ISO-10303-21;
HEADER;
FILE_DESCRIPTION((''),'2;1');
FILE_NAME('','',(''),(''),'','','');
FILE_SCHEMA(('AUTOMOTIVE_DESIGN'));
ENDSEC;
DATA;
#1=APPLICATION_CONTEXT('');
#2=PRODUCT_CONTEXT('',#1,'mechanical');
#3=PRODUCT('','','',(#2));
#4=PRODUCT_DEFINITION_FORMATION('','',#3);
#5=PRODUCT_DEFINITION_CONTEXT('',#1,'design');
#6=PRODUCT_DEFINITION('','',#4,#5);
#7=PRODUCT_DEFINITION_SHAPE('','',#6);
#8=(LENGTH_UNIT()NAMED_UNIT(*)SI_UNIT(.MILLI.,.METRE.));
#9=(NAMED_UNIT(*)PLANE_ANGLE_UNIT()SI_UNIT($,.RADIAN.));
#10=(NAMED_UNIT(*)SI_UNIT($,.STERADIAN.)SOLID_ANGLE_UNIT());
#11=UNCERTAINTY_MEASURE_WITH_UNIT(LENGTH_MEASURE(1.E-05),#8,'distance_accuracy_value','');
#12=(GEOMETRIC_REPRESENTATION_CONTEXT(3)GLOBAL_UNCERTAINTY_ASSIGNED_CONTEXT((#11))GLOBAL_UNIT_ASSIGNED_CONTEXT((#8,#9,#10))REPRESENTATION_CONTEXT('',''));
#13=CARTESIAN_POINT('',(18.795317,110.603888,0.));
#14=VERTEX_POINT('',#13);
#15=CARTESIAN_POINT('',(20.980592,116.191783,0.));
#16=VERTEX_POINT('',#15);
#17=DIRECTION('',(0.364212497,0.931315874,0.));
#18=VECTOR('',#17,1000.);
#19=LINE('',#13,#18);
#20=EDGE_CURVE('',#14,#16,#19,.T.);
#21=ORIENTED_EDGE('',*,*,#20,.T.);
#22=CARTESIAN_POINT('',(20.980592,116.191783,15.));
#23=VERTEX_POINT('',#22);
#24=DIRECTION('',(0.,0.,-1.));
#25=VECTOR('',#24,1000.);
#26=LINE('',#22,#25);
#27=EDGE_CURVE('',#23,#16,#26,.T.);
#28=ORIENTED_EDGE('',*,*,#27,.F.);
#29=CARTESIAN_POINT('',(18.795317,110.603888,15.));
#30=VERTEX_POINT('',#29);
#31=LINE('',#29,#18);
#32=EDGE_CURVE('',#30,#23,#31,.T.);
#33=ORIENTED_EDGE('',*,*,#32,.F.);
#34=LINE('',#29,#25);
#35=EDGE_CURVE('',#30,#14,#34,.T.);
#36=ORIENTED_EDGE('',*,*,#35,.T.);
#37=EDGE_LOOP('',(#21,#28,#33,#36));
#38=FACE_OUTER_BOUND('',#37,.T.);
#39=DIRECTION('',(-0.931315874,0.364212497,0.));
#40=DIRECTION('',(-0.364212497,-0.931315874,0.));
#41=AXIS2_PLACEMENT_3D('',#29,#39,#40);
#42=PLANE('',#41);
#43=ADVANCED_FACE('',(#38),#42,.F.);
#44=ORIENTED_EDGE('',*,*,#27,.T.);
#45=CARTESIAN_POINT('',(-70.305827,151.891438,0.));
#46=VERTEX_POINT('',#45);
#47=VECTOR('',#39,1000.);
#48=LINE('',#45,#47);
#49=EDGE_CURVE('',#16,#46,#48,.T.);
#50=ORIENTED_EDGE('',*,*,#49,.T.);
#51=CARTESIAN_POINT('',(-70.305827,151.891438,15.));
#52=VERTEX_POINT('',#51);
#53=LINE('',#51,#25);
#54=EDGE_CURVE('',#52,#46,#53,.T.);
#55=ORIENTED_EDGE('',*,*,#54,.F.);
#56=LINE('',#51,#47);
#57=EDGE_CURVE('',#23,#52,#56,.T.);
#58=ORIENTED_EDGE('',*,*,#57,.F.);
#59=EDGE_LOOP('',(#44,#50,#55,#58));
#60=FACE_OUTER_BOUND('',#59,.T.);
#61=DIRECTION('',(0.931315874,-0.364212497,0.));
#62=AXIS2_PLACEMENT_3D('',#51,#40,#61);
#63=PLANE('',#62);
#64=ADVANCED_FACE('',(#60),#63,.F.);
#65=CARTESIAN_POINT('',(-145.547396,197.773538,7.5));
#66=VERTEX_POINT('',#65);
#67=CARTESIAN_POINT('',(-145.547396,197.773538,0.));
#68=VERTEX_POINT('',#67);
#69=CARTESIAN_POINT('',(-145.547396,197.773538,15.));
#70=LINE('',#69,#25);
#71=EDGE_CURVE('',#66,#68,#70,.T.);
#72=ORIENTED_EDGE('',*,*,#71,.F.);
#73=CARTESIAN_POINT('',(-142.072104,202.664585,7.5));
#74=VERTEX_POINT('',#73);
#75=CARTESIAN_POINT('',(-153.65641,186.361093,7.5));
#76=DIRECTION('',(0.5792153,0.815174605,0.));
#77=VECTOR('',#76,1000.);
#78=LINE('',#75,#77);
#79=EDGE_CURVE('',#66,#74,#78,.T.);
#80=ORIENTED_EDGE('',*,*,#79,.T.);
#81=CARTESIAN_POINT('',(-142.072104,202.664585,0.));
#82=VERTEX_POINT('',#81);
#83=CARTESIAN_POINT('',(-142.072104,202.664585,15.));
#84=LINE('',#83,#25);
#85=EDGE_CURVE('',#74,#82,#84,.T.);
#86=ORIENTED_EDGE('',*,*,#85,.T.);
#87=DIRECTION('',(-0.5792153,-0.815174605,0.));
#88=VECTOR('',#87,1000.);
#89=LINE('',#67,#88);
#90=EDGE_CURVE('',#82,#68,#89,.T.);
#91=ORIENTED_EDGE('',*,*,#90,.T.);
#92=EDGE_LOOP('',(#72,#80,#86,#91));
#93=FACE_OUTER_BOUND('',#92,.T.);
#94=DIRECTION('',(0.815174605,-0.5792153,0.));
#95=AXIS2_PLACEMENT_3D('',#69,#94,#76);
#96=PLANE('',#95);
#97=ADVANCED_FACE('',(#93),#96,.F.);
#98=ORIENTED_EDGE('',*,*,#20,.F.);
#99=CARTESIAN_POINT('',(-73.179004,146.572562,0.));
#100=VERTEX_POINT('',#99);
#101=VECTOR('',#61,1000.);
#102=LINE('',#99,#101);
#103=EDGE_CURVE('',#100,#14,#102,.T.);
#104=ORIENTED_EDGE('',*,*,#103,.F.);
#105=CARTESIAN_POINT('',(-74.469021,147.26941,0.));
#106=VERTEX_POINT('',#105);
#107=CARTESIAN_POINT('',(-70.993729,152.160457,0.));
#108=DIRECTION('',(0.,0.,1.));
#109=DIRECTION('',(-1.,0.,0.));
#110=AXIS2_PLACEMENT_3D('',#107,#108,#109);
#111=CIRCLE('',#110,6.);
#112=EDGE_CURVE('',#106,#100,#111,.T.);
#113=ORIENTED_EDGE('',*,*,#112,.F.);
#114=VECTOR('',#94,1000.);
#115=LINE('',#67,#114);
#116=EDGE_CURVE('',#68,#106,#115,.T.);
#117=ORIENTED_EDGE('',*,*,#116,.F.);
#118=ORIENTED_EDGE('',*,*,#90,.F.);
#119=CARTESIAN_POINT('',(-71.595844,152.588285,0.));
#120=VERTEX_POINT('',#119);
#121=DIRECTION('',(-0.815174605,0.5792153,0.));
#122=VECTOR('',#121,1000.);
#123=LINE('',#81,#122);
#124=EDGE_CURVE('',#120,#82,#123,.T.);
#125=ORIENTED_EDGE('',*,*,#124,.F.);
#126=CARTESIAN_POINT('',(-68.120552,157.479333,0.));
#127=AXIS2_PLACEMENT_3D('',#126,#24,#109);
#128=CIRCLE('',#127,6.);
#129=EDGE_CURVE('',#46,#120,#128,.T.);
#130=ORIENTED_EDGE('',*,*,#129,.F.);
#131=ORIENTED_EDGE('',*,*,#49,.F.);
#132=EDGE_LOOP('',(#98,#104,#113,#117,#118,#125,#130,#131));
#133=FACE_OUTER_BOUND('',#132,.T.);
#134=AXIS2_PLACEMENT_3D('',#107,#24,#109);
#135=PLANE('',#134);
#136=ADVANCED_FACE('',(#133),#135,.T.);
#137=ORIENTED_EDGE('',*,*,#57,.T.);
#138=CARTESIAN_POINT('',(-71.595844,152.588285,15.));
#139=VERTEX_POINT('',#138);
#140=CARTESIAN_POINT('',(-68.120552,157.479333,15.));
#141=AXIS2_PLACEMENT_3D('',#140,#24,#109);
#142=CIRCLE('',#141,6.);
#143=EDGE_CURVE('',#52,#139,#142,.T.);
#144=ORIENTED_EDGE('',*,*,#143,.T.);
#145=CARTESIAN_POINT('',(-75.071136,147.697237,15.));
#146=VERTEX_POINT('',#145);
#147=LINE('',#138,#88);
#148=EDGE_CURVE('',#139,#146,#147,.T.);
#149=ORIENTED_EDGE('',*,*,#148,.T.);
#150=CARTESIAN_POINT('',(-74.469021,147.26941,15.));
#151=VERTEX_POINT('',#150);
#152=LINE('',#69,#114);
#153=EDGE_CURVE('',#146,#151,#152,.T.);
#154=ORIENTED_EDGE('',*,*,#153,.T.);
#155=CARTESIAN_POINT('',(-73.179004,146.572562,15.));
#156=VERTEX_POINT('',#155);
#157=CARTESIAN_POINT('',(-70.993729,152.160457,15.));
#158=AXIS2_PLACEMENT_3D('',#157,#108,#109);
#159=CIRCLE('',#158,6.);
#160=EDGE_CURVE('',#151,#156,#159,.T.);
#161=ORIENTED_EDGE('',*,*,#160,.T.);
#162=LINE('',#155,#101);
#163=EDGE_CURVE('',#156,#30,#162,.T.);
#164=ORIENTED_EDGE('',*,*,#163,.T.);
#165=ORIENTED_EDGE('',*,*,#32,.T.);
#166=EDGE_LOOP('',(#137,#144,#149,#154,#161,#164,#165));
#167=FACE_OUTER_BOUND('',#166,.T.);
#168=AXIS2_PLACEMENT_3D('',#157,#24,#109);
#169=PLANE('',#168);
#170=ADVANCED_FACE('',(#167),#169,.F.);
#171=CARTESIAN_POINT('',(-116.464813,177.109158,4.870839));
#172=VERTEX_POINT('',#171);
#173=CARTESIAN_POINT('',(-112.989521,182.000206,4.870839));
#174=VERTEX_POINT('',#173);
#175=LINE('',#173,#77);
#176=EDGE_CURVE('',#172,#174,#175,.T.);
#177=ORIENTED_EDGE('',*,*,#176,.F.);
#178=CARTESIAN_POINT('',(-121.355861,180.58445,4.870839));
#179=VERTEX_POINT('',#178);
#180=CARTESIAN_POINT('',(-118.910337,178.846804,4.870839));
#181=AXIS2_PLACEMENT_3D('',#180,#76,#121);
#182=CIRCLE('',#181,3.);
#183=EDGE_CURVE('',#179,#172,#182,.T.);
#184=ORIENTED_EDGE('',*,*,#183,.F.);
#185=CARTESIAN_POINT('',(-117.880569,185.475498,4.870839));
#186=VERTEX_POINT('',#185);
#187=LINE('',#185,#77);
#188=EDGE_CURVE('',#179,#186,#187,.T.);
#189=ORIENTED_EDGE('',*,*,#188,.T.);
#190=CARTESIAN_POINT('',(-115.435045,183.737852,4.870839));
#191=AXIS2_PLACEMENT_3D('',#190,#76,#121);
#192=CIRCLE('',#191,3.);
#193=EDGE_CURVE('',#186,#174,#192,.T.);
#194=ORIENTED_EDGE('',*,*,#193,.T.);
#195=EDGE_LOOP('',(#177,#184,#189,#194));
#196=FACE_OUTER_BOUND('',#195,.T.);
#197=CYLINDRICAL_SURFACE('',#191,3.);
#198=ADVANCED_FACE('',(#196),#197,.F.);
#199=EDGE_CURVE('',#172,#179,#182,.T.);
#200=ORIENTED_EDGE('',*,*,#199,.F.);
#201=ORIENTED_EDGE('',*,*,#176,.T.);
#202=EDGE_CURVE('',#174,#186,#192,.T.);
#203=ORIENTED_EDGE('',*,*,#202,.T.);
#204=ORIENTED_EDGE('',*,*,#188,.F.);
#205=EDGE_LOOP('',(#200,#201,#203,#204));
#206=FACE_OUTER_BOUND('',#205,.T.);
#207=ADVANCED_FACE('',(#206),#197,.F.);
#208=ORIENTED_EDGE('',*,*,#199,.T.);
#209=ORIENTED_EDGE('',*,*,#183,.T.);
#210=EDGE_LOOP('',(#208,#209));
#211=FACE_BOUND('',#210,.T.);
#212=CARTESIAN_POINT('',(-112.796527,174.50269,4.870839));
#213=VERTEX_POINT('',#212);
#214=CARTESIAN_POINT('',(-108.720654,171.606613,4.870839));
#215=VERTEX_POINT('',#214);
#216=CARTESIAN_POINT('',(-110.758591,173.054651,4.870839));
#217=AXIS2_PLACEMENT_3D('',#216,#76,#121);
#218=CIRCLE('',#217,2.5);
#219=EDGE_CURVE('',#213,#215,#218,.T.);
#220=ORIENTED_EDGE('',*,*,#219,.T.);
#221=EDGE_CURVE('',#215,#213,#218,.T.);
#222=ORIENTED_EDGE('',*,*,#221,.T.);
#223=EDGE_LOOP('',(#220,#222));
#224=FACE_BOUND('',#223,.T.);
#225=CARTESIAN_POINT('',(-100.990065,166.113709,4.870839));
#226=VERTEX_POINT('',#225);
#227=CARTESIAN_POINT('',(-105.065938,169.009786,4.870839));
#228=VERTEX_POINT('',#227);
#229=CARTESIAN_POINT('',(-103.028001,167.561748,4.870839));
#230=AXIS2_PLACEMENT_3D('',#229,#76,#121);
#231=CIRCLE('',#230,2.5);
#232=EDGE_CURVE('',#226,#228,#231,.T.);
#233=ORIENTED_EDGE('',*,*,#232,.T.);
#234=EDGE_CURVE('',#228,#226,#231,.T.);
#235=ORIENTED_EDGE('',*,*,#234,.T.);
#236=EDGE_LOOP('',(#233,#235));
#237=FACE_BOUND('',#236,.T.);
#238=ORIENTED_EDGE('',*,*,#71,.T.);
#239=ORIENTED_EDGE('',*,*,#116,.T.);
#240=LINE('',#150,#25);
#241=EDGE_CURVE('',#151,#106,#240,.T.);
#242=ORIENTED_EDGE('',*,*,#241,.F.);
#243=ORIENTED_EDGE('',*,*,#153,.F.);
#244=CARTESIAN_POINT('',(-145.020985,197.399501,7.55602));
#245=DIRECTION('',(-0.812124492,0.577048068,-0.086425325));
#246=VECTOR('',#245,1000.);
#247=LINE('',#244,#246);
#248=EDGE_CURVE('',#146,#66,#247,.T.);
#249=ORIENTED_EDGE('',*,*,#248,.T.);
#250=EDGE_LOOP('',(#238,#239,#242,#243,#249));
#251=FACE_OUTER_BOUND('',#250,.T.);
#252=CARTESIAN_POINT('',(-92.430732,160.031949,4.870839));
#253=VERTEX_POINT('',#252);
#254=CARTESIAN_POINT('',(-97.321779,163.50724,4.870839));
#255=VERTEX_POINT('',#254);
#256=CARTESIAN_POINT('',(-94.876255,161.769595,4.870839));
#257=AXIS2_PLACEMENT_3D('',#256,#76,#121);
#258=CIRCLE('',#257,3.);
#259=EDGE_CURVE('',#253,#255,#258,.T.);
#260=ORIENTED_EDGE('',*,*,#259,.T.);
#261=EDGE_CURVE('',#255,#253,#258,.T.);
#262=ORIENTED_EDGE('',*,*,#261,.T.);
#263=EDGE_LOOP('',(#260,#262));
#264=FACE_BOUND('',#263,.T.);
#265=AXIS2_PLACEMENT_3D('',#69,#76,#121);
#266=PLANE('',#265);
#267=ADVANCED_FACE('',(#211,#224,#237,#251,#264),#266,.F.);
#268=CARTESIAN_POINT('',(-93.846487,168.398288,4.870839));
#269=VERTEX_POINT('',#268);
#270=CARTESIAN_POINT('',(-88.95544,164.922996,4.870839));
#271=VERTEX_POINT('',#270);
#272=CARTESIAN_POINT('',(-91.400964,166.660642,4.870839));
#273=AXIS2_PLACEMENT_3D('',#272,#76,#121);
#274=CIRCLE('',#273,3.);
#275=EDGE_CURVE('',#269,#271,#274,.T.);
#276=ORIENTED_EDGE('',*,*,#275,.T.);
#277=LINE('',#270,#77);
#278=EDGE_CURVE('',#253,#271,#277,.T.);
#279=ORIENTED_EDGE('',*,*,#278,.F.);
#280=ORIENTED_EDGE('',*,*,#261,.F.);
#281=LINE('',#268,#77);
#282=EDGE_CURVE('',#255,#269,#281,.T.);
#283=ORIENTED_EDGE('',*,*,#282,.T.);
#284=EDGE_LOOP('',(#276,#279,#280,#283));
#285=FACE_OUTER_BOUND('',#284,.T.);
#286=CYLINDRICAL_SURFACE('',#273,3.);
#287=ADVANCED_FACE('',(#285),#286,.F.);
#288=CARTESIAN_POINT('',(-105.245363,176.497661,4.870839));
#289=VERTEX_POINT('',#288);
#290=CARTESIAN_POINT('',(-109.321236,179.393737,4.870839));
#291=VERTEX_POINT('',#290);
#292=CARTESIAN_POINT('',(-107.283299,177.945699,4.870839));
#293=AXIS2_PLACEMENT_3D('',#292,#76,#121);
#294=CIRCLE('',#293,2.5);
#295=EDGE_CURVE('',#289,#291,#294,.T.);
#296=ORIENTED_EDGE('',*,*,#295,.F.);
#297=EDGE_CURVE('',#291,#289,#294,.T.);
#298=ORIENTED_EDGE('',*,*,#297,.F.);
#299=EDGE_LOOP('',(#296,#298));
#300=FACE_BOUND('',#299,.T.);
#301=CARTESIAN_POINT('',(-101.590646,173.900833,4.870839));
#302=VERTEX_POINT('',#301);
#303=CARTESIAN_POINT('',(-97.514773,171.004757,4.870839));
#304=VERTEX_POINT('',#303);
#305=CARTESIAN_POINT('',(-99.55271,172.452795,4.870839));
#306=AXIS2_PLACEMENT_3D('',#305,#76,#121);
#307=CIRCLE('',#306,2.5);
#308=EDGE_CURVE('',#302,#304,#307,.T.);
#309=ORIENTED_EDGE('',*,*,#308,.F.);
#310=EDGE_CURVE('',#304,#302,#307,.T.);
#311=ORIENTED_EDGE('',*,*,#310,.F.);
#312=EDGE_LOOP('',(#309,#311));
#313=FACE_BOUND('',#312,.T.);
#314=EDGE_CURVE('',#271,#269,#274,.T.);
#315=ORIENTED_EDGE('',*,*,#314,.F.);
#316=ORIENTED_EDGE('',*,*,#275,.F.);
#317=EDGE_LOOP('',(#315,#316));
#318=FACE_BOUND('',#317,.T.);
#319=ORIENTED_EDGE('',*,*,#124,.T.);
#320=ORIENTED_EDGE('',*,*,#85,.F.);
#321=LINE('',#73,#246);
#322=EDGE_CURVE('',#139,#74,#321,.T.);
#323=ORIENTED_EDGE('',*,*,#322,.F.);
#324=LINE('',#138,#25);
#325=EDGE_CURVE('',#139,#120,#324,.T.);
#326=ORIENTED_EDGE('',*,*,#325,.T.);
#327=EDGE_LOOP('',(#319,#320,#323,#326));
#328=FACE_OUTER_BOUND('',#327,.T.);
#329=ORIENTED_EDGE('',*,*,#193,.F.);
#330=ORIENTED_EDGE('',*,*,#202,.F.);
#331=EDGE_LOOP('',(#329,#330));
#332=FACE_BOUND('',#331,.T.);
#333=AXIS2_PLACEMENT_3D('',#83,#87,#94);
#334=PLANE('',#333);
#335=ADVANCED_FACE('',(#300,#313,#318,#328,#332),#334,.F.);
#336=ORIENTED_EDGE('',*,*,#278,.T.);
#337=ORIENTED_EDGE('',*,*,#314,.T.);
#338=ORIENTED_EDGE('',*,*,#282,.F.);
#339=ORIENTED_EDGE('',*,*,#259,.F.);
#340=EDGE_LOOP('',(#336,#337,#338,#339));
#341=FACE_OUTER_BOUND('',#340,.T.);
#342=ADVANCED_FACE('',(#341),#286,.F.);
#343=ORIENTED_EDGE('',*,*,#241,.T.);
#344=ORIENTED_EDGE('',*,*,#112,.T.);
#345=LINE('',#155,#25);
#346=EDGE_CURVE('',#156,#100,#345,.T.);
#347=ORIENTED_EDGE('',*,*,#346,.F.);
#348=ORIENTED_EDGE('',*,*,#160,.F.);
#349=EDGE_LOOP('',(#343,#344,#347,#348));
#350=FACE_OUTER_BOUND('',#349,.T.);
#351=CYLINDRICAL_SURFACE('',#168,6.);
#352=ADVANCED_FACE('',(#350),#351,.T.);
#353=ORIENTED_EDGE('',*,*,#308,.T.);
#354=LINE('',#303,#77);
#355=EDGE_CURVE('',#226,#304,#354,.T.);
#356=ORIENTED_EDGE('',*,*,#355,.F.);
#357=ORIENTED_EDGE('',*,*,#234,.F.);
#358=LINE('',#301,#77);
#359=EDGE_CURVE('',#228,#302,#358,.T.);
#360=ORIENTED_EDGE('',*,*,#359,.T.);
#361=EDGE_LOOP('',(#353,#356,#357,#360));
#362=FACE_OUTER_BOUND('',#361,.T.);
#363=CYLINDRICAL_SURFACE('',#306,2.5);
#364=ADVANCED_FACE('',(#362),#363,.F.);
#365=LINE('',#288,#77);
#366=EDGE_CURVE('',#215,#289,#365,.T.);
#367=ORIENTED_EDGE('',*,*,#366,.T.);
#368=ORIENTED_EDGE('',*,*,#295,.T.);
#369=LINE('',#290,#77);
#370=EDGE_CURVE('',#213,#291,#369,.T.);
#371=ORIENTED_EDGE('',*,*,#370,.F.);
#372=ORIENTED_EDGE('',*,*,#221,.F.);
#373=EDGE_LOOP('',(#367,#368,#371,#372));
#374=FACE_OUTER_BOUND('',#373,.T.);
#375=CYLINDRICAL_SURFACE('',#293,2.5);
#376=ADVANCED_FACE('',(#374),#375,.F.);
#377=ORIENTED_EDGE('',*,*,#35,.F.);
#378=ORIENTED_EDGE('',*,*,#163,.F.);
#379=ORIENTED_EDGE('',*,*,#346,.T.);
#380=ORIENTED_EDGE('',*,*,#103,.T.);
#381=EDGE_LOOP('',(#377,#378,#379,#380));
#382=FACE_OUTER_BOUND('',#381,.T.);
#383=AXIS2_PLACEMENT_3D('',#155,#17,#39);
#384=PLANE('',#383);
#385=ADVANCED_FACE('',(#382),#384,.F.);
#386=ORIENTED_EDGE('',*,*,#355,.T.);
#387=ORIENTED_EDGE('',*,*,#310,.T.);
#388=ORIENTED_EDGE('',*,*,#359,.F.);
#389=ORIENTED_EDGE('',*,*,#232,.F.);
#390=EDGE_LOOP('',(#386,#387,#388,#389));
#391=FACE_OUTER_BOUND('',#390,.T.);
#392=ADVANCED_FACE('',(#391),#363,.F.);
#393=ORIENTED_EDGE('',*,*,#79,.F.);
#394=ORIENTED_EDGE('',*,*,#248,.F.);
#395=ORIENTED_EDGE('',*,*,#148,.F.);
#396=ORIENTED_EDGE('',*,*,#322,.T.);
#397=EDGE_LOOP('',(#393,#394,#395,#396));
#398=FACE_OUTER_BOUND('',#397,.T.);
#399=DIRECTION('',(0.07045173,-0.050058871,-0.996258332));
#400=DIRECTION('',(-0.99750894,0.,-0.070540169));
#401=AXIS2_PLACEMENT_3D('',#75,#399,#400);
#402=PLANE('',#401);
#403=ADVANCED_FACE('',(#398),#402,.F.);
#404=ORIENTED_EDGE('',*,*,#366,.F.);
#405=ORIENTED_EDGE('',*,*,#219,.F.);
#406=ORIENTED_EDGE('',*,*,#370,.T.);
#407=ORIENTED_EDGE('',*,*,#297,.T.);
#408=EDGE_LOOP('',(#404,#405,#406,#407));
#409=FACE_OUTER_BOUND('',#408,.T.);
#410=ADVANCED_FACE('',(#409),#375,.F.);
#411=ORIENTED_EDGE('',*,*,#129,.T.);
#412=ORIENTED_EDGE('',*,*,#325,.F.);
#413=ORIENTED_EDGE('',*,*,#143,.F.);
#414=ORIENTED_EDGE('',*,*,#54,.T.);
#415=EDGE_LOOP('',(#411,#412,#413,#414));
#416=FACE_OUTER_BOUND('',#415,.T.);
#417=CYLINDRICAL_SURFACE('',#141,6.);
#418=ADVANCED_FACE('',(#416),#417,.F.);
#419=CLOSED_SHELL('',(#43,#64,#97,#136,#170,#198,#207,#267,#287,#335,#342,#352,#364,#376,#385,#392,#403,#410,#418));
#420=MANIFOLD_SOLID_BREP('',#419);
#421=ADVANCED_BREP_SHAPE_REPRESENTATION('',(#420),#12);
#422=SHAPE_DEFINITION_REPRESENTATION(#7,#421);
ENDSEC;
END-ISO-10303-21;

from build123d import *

# Parameters (mm, degrees)
EXTRUDE_1_DEPTH     = 15
CUT_EXTRUDE_1_DEPTH = 20
MM_1_D              = 6
HOLE_WIZARD_M6_1_D  = 5


with BuildPart() as part:
    # 草图1 → 凸台-拉伸1 (new body)
    with BuildSketch(Plane.XY):
        with BuildLine():
            Line((-145.547396155, 197.773537563), (-142.072104357, 202.664585193))
            Line((-142.072104357, 202.664585193), (-71.595844229, 152.588285115))
            ThreePointArc((-71.595844229, 152.588285115), (-70.97220164, 152.200308518), (-70.305827411, 151.891437501))
            Line((-70.305827411, 151.891437501), (20.980591756, 116.19178332))
            Line((20.980591756, 116.19178332), (18.795316776, 110.603888076))
            Line((18.795316776, 110.603888076), (-73.179003731, 146.5725619))
            ThreePointArc((-73.179003731, 146.5725619), (-73.84537796, 146.881432918), (-74.469020549, 147.269409515))
            Line((-74.469020549, 147.269409515), (-145.547396155, 197.773537563))
        make_face()
    extrude(amount=EXTRUDE_1_DEPTH)

    # 草图3 → 切除-拉伸1 (cut)
    with BuildSketch(Plane(origin=(48.026613519, 67.591577297, 0), x_dir=(0.8151746049568696, -0.5792152997231786, 0), z_dir=(0.5792152997231786, 0.8151746049568696, 0))):
        Polygon((-233.2, -7.5), (-146.744583334, -15), (-233.2, -15), align=None)
    extrude(amount=-CUT_EXTRUDE_1_DEPTH, mode=Mode.SUBTRACT)

    # 大小mm 暗销孔1 (through all)
    with Locations(Plane(origin=(48.026613519, 67.591577297, 0), x_dir=(0.8151746049568697, -0.5792152997231785, 0), z_dir=(0.5792152997231785, 0.8151746049568697, 0))):
        with Locations((-200.523492287, -4.870838518), (-171.040138216, -4.870838518)):
            Hole(MM_1_D / 2)

    # M6 螺纹孔1 (through all)
    with Locations(Plane(origin=(48.026613519, 67.591577297, 0), x_dir=(0.8151746049568697, -0.5792152997231785, 0), z_dir=(0.5792152997231785, 0.8151746049568697, 0))):
        with Locations((-190.523492287, -4.870838518), (-181.040138216, -4.870838518)):
            Hole(HOLE_WIZARD_M6_1_D / 2)


solid = part.part
